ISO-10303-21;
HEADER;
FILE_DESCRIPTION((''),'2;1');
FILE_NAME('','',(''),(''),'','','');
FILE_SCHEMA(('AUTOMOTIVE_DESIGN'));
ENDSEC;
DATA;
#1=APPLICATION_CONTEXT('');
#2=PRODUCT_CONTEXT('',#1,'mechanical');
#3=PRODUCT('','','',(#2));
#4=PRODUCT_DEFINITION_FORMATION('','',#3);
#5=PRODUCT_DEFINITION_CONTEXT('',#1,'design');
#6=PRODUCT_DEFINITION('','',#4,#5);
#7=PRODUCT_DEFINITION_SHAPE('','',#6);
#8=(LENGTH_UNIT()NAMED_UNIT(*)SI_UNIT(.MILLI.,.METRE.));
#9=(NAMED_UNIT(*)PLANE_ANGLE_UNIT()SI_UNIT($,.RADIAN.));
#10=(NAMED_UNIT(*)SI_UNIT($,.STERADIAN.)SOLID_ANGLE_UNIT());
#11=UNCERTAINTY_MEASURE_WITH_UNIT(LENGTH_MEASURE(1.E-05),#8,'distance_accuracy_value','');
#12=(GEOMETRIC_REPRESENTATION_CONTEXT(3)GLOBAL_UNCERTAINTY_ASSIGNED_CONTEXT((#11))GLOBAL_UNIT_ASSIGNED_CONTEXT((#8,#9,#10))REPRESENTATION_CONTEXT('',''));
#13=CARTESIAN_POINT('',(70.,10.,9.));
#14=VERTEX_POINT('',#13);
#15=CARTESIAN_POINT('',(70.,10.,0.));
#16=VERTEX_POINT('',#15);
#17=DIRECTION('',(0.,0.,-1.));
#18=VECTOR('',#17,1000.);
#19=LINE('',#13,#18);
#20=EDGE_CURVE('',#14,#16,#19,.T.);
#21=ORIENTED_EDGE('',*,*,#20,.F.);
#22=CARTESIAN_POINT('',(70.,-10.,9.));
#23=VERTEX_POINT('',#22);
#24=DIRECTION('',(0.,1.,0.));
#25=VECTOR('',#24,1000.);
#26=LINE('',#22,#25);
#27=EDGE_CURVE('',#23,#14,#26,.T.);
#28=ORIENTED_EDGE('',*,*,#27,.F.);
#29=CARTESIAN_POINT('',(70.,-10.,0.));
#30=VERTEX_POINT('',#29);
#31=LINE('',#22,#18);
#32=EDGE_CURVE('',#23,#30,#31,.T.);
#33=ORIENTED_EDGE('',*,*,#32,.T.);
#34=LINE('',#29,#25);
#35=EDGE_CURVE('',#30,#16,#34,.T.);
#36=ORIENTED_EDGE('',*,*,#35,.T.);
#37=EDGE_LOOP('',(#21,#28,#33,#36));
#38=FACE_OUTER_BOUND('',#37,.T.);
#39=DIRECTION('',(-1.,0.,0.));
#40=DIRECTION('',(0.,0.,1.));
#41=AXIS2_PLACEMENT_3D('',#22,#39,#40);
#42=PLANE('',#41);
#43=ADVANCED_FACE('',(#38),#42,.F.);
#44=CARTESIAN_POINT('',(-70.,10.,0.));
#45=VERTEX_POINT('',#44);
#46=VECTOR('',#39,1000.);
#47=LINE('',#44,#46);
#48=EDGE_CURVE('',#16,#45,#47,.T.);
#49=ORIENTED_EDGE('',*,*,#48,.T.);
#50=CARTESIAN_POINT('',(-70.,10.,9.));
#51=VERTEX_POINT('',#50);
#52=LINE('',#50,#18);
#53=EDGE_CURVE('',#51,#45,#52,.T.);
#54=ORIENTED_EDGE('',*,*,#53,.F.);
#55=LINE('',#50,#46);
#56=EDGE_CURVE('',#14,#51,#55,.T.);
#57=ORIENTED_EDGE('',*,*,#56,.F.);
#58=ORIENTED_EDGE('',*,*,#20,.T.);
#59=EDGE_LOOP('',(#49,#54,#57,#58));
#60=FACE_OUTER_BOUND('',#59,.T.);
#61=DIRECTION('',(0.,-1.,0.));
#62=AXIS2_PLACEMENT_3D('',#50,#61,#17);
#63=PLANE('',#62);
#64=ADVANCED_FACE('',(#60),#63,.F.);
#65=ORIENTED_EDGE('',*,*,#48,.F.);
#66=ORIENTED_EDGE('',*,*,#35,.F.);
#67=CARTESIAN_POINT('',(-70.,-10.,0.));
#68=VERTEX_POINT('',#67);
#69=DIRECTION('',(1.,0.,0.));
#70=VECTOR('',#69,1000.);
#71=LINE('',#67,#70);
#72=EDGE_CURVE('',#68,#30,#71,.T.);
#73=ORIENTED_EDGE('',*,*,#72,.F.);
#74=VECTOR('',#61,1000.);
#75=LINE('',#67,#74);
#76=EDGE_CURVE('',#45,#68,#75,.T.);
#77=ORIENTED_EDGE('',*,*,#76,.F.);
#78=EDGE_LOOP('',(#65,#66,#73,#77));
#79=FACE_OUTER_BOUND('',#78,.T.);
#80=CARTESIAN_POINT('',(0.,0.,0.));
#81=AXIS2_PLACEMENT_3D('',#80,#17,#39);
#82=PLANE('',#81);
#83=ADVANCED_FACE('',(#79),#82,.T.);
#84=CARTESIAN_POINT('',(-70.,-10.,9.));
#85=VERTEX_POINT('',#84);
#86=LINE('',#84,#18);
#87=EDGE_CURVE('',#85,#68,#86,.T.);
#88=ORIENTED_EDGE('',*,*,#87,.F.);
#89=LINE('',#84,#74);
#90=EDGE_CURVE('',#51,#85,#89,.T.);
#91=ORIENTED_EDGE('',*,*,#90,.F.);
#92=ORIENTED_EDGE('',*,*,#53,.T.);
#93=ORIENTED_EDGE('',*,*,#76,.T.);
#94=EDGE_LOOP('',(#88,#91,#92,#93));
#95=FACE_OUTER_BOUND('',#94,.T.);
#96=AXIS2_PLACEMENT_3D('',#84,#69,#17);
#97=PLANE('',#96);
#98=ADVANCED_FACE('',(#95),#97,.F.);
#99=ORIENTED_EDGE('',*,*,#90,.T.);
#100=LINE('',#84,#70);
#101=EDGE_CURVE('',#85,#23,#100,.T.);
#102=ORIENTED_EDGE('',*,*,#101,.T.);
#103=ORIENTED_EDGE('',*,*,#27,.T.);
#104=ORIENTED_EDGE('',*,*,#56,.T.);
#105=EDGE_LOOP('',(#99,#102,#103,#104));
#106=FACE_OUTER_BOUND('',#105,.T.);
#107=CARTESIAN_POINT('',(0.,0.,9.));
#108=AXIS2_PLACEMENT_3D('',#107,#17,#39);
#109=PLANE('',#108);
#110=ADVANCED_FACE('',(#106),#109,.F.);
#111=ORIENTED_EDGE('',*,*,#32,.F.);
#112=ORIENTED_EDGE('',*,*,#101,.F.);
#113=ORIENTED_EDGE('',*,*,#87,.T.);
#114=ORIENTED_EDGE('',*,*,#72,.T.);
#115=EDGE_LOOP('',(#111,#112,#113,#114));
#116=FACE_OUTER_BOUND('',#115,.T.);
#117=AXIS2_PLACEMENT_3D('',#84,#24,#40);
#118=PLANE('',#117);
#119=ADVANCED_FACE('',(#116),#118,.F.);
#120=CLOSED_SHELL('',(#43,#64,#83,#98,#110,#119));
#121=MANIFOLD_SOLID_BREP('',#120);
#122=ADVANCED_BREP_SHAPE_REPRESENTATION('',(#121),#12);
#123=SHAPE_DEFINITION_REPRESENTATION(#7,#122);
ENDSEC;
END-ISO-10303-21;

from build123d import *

# Parameters (mm, degrees)
SKETCH_1_W      = 140
SKETCH_1_H      = 20
EXTRUDE_1_DEPTH = 9


with BuildPart() as part:
    # 草图1 → 凸台-拉伸1 (new body)
    with BuildSketch(Plane.XY):
        Rectangle(SKETCH_1_W, SKETCH_1_H)
    extrude(amount=EXTRUDE_1_DEPTH)


solid = part.part
